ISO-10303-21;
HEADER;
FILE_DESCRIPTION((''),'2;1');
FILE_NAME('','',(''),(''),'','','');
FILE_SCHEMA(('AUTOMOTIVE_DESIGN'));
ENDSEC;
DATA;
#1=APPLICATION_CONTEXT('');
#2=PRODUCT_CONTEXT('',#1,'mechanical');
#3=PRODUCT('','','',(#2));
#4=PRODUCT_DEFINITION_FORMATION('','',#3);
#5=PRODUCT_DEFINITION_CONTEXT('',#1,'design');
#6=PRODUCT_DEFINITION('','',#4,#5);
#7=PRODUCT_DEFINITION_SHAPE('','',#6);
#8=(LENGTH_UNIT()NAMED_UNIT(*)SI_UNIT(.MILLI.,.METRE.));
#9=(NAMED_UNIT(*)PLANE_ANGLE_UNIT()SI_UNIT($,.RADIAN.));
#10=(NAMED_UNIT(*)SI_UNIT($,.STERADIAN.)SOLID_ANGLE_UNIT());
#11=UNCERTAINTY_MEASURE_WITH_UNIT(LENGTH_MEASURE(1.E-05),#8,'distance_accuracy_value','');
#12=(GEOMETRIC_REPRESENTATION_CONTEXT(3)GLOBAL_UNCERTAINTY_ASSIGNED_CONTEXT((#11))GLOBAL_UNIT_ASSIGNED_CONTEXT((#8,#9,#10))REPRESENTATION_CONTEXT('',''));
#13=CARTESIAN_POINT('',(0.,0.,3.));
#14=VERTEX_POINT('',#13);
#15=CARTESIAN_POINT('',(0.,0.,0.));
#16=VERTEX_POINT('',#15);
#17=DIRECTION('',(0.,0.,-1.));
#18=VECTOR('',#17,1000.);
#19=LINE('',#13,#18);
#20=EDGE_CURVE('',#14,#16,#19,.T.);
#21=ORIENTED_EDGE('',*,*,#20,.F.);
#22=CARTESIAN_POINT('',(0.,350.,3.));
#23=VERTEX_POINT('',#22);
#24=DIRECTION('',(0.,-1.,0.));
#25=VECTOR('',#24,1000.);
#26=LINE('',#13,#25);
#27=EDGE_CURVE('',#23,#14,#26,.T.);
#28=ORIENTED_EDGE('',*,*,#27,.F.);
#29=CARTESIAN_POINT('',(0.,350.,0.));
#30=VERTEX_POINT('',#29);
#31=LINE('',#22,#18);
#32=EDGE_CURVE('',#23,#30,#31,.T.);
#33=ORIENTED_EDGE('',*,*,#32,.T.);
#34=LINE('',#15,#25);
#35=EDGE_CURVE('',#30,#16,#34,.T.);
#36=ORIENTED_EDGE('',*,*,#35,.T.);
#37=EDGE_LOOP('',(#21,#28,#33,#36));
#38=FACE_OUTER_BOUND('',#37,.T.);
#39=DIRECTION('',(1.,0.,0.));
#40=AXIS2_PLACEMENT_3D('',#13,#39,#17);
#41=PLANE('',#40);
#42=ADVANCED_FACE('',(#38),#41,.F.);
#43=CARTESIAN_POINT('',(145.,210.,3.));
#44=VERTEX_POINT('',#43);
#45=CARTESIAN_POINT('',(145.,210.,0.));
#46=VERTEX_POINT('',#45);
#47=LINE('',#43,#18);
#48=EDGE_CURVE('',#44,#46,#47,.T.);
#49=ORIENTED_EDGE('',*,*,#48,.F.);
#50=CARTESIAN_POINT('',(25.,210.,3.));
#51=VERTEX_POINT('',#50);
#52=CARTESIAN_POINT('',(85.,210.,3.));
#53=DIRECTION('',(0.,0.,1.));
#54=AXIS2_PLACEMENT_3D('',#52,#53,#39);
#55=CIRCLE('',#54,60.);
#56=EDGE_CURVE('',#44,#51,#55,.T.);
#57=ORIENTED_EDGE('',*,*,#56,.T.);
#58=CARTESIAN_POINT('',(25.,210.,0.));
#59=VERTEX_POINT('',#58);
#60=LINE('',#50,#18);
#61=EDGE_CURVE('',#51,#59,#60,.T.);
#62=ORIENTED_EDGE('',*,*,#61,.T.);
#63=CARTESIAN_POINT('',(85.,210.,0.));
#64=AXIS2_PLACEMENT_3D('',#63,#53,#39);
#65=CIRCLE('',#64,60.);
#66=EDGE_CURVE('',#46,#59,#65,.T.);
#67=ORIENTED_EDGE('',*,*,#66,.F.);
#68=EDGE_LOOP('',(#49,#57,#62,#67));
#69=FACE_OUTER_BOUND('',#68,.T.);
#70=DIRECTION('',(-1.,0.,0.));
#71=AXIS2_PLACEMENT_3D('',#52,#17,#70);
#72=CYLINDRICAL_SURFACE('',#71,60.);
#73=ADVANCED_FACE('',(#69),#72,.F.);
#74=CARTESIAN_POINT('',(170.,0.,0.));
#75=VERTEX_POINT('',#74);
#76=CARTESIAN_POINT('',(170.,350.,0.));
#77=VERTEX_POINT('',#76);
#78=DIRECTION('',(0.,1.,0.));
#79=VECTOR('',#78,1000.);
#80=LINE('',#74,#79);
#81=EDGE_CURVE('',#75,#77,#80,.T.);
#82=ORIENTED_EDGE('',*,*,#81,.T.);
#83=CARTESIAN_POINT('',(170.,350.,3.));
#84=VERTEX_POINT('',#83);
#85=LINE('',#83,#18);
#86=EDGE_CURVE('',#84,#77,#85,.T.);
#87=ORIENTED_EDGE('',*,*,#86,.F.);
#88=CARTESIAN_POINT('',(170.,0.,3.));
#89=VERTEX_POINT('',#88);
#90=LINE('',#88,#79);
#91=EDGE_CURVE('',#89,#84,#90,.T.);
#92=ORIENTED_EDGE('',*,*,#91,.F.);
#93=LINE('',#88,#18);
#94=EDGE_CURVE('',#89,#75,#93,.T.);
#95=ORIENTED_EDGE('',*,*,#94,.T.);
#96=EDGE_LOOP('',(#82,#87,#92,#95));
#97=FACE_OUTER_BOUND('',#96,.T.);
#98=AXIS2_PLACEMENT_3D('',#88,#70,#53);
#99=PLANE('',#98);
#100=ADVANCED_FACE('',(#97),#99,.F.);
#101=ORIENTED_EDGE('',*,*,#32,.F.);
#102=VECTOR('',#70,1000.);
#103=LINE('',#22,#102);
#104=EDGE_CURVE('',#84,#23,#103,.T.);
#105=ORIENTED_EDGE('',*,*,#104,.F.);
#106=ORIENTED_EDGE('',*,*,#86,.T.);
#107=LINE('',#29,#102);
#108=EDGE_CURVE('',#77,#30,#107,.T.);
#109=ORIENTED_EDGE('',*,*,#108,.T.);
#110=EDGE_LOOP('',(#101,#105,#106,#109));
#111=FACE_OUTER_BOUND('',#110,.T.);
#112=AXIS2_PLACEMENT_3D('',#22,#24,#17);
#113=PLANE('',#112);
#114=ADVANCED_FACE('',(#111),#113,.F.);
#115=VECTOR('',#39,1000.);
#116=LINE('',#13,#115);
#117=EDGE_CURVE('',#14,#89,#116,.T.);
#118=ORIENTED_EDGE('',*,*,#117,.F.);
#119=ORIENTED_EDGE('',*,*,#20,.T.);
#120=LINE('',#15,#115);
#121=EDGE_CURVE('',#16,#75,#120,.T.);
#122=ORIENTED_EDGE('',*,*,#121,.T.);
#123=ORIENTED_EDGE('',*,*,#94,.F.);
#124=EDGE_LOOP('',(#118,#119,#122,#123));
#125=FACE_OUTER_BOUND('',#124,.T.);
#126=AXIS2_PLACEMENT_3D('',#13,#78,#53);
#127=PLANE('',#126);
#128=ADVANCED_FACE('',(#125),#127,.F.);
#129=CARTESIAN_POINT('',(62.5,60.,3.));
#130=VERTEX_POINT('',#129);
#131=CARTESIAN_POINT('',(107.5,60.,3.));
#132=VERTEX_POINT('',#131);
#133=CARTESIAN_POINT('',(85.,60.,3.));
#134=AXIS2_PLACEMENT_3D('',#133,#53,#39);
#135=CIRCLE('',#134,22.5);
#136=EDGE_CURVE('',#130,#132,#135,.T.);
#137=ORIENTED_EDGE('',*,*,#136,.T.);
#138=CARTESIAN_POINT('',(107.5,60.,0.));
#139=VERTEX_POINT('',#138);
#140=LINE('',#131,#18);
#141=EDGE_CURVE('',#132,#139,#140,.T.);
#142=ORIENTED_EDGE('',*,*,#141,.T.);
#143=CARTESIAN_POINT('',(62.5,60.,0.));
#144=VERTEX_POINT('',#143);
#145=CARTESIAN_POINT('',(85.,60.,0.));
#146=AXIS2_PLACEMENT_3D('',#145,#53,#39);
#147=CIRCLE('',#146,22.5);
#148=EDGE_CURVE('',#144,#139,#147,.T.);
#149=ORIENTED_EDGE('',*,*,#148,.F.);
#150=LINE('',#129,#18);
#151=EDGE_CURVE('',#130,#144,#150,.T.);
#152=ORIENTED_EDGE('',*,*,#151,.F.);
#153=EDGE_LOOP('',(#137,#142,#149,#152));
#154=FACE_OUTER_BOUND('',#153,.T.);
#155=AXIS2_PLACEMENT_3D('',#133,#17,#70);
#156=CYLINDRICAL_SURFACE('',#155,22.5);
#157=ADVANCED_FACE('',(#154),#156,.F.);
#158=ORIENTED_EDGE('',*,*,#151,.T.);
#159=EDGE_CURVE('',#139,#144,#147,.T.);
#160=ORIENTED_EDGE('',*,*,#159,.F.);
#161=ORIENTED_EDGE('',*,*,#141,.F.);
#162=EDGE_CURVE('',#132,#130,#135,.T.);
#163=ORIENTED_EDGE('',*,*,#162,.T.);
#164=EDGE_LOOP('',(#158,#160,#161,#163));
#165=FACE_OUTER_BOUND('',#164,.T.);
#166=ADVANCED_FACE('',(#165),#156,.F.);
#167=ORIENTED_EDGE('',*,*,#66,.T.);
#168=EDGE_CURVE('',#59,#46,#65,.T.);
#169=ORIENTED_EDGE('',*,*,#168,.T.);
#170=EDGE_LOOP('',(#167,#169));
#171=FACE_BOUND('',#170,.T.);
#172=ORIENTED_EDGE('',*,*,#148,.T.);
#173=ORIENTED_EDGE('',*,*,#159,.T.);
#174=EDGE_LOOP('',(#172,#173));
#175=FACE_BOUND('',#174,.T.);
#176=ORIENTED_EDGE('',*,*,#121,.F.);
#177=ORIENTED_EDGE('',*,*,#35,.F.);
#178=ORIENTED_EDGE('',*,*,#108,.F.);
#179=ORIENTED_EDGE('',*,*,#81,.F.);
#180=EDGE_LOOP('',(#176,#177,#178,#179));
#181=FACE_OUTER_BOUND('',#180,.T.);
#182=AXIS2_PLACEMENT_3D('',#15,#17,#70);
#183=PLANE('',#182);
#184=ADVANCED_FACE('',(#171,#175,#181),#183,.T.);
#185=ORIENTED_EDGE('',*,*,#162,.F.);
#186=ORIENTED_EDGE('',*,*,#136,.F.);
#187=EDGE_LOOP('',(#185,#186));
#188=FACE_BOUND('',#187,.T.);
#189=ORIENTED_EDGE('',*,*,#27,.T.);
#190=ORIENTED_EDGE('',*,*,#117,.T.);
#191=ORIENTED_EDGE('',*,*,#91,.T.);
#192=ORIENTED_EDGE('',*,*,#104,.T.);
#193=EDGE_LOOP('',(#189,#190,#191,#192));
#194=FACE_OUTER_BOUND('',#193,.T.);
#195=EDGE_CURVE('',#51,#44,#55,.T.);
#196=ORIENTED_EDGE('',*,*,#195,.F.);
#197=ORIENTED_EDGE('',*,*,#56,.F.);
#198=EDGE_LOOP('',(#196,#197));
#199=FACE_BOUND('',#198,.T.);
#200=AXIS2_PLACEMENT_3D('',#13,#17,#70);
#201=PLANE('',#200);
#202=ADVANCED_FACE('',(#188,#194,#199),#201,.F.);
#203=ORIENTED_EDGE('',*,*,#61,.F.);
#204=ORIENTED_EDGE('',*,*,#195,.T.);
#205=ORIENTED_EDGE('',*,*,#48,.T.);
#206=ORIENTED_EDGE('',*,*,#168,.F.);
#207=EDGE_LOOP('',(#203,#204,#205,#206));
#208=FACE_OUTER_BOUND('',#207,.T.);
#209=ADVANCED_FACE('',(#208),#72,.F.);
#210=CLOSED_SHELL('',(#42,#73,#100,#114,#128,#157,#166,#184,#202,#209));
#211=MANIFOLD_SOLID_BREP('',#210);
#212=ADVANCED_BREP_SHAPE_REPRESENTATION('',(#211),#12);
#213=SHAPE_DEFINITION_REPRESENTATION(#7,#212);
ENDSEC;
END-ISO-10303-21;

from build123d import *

# Parameters (mm, degrees)
SKETCH1_W           = 170
SKETCH1_H           = 350
SKETCH1_R           = 60
SKETCH1_R_2         = 22.5
BOSS_EXTRUDE1_DEPTH = 3


with BuildPart() as part:
    # Sketch1 → Boss-Extrude1 (new body)
    with BuildSketch(Plane.XY):
        with Locations((85, 175)):
            Rectangle(SKETCH1_W, SKETCH1_H)
        with Locations((85, 210)):
            Circle(SKETCH1_R, mode=Mode.SUBTRACT)
        with Locations((85, 60)):
            Circle(SKETCH1_R_2, mode=Mode.SUBTRACT)
    extrude(amount=BOSS_EXTRUDE1_DEPTH)


solid = part.part
